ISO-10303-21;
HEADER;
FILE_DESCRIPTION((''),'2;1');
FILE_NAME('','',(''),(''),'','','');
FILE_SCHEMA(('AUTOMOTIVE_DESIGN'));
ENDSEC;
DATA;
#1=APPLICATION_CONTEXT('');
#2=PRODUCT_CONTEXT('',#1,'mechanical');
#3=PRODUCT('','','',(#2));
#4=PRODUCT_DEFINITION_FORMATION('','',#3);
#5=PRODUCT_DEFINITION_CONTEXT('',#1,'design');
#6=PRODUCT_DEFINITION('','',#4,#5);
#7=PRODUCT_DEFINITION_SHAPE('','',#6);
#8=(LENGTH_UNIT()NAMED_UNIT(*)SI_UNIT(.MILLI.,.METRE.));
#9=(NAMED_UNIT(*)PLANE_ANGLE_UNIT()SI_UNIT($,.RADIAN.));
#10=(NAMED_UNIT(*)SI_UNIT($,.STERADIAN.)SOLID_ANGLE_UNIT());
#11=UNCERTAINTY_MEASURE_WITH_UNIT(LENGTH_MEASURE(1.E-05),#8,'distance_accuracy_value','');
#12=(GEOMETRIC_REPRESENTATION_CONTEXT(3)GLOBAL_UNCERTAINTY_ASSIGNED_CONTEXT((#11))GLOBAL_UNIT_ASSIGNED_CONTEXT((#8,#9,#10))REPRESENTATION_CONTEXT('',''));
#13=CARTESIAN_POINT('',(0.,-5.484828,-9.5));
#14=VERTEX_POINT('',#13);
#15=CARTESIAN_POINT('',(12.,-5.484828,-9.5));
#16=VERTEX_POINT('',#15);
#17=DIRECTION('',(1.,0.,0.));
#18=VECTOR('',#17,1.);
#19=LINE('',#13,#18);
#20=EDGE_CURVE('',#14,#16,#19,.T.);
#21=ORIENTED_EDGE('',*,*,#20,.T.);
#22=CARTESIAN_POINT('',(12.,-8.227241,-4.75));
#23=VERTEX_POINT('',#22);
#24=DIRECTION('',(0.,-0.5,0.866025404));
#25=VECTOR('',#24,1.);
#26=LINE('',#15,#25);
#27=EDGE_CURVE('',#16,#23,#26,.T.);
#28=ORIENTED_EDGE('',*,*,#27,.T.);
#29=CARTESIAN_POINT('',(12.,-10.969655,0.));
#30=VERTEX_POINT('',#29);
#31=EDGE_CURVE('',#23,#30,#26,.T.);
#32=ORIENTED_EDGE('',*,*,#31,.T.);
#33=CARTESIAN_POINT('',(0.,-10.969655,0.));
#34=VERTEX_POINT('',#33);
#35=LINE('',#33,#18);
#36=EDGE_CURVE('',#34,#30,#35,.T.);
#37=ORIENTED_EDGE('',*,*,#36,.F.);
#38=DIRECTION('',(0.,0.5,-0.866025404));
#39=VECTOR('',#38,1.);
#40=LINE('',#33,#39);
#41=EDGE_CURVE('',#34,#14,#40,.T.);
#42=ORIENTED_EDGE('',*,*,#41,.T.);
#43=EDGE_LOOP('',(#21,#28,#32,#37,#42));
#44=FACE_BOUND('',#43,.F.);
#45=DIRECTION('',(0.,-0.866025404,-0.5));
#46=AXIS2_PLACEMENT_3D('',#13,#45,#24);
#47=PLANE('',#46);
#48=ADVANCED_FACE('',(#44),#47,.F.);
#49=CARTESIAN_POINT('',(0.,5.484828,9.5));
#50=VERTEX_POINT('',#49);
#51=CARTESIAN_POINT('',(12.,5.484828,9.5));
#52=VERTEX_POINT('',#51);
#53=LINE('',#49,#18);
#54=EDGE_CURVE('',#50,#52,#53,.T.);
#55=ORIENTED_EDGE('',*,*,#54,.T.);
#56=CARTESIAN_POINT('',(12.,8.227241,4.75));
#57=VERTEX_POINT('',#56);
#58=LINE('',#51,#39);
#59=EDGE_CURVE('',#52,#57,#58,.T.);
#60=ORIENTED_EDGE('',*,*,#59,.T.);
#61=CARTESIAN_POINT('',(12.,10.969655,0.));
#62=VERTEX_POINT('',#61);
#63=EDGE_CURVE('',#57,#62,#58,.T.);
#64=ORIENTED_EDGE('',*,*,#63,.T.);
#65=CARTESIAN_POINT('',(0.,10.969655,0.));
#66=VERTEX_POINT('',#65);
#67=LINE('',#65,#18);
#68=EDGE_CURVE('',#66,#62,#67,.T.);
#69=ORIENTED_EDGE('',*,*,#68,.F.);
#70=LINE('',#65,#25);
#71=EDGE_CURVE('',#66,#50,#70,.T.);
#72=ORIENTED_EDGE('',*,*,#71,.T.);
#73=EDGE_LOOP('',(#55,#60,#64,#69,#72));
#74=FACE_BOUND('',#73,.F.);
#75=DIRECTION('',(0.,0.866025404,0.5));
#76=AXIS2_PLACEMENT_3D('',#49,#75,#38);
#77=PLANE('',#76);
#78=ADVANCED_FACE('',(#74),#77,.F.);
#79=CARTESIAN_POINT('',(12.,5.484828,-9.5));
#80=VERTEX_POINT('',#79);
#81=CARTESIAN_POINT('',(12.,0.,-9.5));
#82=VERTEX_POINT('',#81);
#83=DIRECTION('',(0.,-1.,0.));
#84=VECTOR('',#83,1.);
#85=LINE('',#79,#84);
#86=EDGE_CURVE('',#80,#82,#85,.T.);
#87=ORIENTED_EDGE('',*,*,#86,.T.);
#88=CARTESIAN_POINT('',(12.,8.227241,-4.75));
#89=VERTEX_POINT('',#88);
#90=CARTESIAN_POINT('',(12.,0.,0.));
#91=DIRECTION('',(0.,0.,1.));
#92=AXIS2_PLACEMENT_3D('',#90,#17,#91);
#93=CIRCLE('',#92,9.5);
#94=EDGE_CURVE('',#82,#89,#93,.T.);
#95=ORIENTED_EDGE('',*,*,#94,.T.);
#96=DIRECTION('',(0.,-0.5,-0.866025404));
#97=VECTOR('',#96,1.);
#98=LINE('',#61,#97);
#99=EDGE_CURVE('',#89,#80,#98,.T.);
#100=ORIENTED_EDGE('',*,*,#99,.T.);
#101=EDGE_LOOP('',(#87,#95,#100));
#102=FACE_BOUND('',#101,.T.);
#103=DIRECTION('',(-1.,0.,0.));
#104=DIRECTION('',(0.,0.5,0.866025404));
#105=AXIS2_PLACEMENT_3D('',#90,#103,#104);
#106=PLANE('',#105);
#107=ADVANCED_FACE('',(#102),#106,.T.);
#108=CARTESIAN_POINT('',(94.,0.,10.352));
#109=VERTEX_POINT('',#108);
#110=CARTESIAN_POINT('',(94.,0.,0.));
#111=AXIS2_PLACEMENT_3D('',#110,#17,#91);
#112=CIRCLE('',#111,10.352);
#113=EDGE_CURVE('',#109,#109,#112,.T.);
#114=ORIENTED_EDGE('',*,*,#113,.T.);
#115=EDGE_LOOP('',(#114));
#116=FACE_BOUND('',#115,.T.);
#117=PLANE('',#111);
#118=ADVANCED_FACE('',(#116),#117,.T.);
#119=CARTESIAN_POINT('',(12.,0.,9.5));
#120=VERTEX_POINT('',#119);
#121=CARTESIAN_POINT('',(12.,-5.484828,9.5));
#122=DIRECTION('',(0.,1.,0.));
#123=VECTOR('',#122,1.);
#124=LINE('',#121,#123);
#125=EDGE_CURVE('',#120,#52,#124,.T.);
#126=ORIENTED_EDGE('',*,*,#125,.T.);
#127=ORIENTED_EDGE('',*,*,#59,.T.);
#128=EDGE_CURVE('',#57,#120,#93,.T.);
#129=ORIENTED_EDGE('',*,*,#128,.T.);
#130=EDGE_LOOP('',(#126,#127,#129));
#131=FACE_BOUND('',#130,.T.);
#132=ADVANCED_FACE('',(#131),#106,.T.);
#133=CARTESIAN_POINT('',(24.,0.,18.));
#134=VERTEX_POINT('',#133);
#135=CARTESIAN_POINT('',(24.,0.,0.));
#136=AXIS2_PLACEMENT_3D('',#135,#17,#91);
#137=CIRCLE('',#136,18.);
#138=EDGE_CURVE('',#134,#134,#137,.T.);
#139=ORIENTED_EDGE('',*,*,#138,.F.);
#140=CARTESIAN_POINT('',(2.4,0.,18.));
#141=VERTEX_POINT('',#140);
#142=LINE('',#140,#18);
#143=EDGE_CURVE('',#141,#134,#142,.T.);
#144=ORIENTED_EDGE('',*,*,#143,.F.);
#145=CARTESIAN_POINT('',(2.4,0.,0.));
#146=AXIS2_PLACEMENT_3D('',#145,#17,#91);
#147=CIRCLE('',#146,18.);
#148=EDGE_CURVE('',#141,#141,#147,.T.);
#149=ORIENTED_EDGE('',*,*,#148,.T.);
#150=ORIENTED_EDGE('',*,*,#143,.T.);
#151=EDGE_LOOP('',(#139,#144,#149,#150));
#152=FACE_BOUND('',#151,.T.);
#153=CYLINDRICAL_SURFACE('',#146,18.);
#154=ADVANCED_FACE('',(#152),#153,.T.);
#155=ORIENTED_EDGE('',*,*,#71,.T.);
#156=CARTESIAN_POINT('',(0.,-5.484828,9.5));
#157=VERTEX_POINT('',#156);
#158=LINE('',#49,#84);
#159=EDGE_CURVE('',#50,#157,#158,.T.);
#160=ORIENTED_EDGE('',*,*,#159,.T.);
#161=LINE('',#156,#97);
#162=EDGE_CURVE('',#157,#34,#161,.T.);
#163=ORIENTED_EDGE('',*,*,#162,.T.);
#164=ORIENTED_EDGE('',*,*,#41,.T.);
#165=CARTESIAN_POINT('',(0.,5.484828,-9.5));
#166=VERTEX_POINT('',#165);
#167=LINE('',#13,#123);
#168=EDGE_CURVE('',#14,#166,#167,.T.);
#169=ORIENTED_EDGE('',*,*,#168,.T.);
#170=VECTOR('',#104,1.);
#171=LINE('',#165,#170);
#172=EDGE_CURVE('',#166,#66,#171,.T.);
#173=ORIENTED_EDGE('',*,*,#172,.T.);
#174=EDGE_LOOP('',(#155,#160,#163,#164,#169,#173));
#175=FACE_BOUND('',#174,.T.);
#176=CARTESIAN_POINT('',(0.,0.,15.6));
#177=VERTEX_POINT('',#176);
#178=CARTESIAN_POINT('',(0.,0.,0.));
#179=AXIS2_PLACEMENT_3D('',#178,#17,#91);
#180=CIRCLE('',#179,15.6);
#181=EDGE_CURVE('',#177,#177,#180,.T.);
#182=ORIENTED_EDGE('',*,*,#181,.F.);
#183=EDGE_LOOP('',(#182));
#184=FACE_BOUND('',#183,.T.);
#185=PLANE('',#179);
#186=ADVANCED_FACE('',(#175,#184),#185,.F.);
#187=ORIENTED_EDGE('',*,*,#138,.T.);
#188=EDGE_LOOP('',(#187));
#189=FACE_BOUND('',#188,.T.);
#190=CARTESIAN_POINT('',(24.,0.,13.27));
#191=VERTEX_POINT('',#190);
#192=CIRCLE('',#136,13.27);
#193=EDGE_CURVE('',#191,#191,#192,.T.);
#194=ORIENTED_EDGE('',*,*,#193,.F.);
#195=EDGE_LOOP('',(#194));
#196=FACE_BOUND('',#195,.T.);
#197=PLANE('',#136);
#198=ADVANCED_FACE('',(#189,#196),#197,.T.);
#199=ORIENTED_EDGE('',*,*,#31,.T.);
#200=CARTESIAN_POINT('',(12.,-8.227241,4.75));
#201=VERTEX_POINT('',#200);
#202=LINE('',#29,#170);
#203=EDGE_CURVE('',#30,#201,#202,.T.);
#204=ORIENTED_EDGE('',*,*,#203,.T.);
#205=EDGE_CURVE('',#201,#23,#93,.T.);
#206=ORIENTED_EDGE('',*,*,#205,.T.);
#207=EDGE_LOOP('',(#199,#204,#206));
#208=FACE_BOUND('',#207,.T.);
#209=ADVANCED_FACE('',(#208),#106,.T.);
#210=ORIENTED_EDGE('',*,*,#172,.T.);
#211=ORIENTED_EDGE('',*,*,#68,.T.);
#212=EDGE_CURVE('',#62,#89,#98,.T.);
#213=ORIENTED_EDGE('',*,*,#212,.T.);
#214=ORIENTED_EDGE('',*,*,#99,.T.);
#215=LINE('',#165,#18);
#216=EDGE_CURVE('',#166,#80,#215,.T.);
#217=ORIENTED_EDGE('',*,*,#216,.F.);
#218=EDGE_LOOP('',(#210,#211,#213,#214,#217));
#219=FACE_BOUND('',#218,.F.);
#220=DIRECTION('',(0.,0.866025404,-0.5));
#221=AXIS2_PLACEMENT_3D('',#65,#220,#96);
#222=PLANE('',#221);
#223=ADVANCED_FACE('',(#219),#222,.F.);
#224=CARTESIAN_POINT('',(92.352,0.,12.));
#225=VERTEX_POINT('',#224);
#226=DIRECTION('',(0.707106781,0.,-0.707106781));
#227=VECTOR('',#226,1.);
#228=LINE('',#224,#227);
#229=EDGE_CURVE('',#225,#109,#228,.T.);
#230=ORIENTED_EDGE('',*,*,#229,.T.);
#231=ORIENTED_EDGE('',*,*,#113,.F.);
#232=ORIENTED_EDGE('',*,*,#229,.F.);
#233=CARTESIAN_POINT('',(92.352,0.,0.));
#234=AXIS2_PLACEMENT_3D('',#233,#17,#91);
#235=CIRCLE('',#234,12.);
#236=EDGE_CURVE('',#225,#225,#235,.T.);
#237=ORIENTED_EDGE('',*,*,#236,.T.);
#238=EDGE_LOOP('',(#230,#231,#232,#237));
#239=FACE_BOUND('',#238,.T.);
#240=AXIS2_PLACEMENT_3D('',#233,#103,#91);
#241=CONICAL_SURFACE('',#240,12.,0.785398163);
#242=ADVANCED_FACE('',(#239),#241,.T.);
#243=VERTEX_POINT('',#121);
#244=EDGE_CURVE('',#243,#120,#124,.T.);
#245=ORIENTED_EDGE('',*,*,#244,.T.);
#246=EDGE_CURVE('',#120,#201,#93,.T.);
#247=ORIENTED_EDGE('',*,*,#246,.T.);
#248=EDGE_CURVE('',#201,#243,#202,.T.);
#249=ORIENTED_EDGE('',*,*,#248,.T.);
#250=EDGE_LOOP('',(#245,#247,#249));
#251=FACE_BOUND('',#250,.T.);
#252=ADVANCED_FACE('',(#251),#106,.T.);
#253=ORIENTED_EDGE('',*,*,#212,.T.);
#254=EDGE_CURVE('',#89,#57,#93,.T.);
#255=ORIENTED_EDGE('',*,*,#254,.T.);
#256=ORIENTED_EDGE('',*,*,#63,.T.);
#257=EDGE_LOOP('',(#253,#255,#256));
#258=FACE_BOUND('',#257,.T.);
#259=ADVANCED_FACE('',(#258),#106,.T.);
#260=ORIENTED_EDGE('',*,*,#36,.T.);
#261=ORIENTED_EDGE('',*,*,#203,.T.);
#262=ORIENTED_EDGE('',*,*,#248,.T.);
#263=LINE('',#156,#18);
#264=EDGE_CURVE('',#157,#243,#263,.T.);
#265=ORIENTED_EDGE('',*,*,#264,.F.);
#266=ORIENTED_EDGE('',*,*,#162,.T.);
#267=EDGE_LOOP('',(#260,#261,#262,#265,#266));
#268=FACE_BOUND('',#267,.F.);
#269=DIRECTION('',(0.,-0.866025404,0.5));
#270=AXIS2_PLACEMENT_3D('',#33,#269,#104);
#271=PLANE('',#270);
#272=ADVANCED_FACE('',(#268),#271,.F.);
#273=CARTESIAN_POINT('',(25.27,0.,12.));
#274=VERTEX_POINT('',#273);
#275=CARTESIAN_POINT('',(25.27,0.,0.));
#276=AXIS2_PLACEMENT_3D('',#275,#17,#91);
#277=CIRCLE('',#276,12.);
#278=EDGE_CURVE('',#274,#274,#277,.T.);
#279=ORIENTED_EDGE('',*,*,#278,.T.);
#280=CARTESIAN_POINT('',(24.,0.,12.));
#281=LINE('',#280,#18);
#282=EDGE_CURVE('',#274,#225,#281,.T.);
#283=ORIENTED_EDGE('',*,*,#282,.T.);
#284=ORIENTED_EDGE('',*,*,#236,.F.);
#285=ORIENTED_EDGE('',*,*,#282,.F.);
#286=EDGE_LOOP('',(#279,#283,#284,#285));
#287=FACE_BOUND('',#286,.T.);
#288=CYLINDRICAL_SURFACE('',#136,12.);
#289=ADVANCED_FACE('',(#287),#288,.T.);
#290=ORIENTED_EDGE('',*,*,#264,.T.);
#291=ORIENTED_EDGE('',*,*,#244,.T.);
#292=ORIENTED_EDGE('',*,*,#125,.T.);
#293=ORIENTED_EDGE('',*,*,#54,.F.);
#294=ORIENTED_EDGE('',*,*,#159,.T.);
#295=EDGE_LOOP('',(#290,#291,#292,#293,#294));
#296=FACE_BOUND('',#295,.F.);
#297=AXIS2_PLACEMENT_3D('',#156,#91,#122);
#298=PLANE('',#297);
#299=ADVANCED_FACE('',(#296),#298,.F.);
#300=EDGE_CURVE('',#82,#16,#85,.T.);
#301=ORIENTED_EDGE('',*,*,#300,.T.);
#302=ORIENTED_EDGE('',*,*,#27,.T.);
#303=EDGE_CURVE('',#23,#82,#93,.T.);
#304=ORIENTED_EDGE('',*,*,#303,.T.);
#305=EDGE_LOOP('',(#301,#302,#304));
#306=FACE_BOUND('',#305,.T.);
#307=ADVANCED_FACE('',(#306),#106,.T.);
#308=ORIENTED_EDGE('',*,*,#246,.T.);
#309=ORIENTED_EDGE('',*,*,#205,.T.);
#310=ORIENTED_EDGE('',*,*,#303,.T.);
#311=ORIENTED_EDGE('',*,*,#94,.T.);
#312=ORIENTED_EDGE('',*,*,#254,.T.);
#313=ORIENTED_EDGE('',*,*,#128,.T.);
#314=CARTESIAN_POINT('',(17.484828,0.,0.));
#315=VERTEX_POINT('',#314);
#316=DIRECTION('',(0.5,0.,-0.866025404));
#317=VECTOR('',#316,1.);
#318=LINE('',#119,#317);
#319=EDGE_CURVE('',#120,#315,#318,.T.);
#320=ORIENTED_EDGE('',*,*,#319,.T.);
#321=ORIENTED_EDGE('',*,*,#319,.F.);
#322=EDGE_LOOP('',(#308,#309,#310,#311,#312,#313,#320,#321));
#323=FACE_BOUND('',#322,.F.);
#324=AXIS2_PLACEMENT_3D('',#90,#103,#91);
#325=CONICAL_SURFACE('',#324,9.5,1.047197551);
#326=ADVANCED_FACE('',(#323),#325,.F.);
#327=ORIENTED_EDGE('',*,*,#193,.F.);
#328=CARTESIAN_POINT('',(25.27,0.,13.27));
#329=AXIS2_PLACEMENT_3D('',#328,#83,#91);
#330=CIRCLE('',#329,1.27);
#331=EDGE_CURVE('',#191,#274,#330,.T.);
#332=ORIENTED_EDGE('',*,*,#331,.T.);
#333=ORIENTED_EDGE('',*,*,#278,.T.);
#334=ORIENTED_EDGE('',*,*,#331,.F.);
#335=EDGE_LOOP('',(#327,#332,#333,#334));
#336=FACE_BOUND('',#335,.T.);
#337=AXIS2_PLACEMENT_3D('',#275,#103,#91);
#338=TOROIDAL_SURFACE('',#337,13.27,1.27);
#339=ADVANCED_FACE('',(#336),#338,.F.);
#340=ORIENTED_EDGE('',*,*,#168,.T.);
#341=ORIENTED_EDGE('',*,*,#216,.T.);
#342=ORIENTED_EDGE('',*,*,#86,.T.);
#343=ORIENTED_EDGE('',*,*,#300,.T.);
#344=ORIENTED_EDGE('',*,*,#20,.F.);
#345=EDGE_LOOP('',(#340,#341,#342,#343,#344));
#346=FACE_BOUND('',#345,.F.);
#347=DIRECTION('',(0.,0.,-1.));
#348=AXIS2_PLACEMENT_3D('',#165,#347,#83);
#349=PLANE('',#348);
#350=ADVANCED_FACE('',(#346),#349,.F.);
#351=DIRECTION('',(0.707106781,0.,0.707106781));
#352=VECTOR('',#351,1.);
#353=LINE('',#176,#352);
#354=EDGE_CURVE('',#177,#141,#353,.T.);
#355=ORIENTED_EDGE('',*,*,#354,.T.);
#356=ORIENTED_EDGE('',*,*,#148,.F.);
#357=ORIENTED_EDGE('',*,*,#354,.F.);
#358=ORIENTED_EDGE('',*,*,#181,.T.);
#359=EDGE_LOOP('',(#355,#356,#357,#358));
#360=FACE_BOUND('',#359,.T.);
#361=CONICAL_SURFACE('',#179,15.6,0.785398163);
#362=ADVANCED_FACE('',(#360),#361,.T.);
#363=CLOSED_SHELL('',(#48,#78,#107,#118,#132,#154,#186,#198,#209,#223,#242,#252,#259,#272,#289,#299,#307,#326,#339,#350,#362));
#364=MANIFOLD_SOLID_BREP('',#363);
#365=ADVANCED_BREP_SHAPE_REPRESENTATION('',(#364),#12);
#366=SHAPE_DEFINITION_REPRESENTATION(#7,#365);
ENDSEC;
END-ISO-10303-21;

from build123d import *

# Parameters (mm, degrees)
FILLET1_R   = 1.27
HEX_2_DEPTH = 12


with BuildPart() as part:
    # BodySke → Base-Revolve (revolve)
    with BuildSketch(Plane.XY, mode=Mode.PRIVATE) as base_revolve_sk:
        Polygon((0, 0), (0, 15.6), (2.4, 18), (24, 18), (24, 12), (92.352, 12), (94, 10.352), (94, 0), align=None)
    revolve(base_revolve_sk.sketch.rotate(Axis((-31.75, 0, 0), (1, 0, 0)), 90), axis=Axis((-31.75, 0, 0), (1, 0, 0)))

    # Fillet1
    fillet1_edges = [part.edges().sort_by_distance(p)[0] for p in [
        (24, 0, -12),
    ]]
    fillet(fillet1_edges, radius=FILLET1_R)

    # Sketch2 → Hex-PreBroach (revolve, cut)
    with BuildSketch(Plane.XY, mode=Mode.PRIVATE) as hex_prebroach_sk:
        Polygon((0, 9.5), (12, 9.5), (17.484827557, 0), (0, 0), align=None)
    revolve(hex_prebroach_sk.sketch.rotate(Axis((0, 0, 0), (1, 0, 0)), 90), axis=Axis((0, 0, 0), (1, 0, 0)), mode=Mode.SUBTRACT)

    # Sketch3 → Hex 2 (cut)
    with BuildSketch(Plane(origin=(0, 0, 0), x_dir=(0, 0.500000000000001, 0.866025403784438), z_dir=(-1, 0, 0))):
        Polygon((5.484827557, 9.5), (-5.484827557, 9.5), (-10.969655115, 0), (-5.484827557, -9.5), (5.484827557, -9.5), (10.969655115, 0), align=None)
    extrude(amount=-HEX_2_DEPTH, mode=Mode.SUBTRACT)


solid = part.part
